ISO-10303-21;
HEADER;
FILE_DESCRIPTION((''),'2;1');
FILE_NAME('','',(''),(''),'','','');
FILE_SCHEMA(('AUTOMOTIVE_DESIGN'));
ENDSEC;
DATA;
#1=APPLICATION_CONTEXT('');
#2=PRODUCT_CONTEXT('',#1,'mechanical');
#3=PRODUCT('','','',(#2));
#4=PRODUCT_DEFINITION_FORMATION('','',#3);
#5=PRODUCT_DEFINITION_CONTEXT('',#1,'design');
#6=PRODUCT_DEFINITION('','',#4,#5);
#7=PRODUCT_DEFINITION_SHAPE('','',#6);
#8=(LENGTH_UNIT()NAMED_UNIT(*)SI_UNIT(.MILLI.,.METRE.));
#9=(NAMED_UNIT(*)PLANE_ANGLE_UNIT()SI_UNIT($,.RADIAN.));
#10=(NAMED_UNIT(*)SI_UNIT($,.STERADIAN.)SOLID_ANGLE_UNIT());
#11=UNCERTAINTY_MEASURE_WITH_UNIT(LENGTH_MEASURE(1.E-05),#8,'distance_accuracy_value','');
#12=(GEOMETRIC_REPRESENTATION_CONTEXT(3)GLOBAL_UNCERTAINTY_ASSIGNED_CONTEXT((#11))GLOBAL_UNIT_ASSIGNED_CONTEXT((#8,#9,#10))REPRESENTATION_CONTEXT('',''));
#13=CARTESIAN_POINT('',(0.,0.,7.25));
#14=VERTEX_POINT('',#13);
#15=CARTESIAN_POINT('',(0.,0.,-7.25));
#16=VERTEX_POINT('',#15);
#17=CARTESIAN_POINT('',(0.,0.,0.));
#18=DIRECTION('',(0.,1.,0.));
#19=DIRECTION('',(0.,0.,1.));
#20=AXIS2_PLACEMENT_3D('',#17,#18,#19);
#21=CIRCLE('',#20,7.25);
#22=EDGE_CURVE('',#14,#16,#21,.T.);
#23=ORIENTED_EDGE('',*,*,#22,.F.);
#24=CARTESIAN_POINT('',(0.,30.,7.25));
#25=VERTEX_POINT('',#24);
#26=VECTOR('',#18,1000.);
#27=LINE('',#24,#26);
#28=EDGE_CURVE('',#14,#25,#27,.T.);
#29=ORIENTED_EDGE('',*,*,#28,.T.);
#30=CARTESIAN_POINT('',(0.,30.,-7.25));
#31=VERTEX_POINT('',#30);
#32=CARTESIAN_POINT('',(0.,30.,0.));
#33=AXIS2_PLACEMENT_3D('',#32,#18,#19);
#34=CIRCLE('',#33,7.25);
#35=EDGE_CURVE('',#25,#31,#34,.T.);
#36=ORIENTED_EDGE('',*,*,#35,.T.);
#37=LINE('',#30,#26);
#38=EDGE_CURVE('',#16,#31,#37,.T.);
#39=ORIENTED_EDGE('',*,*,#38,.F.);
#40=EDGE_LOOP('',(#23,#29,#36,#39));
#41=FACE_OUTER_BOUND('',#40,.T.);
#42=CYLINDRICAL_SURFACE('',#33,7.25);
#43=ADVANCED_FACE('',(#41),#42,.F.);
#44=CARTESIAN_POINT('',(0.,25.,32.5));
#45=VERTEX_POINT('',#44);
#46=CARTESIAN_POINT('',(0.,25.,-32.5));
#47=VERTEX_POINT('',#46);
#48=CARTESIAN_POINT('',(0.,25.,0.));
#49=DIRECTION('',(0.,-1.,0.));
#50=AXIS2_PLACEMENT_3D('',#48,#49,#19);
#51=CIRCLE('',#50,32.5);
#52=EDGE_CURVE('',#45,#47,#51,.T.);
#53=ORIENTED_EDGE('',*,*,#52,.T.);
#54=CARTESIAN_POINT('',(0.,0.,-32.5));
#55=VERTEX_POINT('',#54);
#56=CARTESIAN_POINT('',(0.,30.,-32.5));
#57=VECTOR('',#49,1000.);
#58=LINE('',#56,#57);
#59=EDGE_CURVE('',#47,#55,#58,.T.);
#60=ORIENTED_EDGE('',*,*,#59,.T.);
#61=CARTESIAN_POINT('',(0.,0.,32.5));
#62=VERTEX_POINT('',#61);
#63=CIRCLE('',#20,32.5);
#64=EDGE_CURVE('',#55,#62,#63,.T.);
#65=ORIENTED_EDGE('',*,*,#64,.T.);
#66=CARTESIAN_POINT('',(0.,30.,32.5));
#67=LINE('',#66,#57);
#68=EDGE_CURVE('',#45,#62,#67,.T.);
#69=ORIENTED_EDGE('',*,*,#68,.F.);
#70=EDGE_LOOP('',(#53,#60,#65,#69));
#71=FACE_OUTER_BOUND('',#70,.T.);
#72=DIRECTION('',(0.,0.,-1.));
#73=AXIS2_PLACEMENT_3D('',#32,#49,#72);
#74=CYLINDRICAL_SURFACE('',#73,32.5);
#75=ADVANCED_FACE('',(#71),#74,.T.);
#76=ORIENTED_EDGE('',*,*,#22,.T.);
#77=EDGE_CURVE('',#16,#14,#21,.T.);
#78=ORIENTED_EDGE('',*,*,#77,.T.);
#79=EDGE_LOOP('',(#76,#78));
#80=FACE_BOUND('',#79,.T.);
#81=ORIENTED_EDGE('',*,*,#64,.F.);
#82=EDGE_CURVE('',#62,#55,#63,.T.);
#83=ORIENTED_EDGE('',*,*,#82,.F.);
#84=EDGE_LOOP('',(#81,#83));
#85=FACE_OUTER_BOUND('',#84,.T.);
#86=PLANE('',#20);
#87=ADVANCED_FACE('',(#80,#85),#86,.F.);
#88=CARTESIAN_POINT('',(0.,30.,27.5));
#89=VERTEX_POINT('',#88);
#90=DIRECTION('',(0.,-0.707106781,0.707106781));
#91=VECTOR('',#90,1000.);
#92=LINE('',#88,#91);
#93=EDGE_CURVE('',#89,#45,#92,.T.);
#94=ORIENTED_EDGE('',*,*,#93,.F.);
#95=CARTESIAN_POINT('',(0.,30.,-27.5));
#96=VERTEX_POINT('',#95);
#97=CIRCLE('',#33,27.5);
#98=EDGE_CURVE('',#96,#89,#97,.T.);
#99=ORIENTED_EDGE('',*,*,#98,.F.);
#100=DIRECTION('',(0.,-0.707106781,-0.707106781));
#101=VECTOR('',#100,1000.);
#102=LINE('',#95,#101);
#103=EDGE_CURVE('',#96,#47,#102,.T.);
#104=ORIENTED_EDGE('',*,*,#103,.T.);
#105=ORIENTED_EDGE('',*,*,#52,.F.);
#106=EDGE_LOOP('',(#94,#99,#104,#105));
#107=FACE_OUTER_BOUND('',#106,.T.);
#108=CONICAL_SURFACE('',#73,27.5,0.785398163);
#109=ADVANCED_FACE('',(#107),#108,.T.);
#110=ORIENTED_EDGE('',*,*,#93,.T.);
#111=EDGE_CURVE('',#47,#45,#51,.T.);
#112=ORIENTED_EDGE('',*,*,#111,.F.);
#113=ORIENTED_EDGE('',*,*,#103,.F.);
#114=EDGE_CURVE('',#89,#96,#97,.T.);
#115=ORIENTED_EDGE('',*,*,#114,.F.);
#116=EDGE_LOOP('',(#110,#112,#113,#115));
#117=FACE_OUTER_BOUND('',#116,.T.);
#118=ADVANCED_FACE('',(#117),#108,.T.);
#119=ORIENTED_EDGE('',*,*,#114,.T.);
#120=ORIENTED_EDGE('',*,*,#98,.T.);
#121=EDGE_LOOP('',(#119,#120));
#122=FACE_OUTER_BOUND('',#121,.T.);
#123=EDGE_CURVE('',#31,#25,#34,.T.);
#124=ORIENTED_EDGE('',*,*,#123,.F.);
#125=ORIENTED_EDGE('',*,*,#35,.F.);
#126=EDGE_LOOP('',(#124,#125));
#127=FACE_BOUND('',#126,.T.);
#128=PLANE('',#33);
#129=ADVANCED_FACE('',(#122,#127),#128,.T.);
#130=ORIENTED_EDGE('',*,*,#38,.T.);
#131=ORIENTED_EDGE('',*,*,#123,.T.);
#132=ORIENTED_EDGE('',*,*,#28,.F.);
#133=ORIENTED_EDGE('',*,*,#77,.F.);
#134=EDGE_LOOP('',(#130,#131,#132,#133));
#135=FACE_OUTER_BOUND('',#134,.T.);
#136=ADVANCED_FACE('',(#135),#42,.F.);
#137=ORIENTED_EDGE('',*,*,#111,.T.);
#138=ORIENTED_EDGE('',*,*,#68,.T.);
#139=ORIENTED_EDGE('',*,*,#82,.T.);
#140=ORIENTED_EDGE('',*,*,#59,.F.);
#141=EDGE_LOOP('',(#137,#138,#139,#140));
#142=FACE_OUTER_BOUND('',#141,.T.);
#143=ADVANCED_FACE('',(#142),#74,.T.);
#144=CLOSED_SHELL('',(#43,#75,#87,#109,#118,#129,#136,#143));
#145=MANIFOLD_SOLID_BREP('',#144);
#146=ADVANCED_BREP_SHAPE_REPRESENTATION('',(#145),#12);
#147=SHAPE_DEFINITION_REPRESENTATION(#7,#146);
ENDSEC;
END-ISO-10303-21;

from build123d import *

# Parameters (mm, degrees)
SKETCH1_R                  = 32.5
BOSS_EXTRUDE1_DEPTH        = 30
CHAMFER1_SIZE              = 5
M16X1_5_TAPPED_HOLE1_D     = 14.5
M16X1_5_TAPPED_HOLE1_DEPTH = 36.5
M16X1_5_TAPPED_HOLE1_TIP   = 4.356239488


with BuildPart() as part:
    # Sketch1 → Boss-Extrude1 (new body)
    with BuildSketch(Plane(origin=(0, 0, 0), x_dir=(1, 0, 0), z_dir=(0, 1, 0))):
        with Locations(Location((0, 0, 0), (0, 0, 270))):
            Circle(SKETCH1_R)
    extrude(amount=BOSS_EXTRUDE1_DEPTH)

    # Chamfer1
    chamfer1_edges = [part.edges().sort_by_distance(p)[0] for p in [
        (0, 30, -32.5),
    ]]
    chamfer(chamfer1_edges, length=CHAMFER1_SIZE)

    # M16x1.5 Tapped Hole1
    with Locations(Plane(origin=(0, 30, 0), x_dir=(1, 0, 0), z_dir=(0, 1, 0))):
        with Locations((0, 0)):
            Hole(M16X1_5_TAPPED_HOLE1_D / 2, depth=M16X1_5_TAPPED_HOLE1_DEPTH)
            with Locations((0, 0, -(M16X1_5_TAPPED_HOLE1_DEPTH + M16X1_5_TAPPED_HOLE1_TIP / 2))):  # 118° drill point
                Cone(0, M16X1_5_TAPPED_HOLE1_D / 2, M16X1_5_TAPPED_HOLE1_TIP, mode=Mode.SUBTRACT)


solid = part.part
